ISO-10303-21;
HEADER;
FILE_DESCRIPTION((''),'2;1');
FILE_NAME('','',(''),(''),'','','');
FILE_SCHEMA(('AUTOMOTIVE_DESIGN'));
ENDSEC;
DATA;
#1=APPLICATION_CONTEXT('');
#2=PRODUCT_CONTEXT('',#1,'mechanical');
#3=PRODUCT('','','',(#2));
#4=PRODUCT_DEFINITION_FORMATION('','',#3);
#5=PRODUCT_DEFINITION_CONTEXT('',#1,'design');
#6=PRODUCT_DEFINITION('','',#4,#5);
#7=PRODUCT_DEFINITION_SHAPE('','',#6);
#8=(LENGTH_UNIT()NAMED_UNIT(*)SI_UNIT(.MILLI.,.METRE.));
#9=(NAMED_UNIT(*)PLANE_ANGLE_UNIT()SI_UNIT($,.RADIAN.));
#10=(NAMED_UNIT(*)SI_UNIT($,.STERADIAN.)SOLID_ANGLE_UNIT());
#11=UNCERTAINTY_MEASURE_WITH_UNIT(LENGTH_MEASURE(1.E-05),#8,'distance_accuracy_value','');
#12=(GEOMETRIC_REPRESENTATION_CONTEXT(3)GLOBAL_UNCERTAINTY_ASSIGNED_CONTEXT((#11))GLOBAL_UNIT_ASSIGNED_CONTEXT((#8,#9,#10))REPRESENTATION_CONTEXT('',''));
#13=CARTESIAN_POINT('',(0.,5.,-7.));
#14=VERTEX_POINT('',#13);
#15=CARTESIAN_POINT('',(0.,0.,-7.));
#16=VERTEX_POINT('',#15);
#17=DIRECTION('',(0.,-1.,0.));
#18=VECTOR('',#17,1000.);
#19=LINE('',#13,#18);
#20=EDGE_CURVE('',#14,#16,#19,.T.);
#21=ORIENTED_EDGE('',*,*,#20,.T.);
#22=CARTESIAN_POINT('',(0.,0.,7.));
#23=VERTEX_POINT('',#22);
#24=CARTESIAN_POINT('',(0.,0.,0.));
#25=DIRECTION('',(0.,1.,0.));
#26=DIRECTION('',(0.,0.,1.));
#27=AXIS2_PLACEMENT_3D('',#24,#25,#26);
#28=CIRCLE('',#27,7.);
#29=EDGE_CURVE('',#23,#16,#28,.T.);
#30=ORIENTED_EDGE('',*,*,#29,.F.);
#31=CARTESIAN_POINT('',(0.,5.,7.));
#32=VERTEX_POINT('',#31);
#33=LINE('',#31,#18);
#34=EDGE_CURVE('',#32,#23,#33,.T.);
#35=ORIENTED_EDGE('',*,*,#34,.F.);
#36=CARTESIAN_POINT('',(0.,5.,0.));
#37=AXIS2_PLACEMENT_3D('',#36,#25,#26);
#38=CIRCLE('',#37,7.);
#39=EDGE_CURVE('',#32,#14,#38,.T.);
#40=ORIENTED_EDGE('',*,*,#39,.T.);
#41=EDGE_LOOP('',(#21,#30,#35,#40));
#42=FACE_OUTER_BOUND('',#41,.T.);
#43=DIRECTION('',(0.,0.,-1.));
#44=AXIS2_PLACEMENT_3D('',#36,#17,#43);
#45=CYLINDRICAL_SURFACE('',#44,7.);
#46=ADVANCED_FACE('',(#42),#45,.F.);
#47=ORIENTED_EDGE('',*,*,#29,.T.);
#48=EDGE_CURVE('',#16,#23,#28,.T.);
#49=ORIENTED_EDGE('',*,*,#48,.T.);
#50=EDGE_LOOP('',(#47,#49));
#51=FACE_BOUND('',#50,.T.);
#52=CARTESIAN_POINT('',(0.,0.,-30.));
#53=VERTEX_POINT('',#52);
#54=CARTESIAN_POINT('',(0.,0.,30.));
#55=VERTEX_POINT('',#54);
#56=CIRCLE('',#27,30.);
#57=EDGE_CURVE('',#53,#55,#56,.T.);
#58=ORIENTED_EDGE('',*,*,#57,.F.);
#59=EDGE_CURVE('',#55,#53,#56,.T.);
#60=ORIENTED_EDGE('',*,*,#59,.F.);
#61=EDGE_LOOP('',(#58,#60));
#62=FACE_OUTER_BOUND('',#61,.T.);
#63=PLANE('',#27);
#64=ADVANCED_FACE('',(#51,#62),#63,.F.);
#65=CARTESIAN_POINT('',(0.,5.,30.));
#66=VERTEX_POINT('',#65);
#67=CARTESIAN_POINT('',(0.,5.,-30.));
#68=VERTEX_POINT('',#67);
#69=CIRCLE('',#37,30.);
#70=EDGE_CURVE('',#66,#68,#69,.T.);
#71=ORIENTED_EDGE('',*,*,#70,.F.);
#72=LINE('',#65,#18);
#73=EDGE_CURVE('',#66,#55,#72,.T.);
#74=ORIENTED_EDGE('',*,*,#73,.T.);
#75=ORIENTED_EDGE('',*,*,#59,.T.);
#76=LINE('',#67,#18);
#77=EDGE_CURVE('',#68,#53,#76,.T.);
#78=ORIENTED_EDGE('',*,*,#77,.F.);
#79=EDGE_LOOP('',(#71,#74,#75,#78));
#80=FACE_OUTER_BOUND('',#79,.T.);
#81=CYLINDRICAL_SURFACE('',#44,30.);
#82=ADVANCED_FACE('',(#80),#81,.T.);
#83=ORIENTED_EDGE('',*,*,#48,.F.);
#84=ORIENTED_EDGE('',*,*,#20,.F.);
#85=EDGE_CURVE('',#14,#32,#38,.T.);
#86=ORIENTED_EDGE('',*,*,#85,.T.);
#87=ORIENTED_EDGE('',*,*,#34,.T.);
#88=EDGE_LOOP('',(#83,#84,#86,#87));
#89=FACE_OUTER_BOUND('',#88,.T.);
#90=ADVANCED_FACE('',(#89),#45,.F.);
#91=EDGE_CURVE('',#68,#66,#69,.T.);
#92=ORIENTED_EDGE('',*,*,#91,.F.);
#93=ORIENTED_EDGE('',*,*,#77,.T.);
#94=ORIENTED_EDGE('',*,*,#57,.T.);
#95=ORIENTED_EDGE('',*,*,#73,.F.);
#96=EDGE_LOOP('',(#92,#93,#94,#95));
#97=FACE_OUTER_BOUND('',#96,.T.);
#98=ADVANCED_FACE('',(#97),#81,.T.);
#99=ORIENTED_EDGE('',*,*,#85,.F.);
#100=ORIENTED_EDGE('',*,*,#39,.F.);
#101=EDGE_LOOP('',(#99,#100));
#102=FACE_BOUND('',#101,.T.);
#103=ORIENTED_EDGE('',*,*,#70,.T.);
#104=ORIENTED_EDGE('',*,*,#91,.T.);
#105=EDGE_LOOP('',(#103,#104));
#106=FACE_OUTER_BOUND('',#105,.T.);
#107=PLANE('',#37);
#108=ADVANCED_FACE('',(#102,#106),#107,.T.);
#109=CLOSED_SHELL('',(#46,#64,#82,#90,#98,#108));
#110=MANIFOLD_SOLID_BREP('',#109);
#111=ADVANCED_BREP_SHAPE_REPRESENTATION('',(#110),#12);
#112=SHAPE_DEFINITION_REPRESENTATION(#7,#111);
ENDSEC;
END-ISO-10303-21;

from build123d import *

# Parameters (mm, degrees)
SKETCH_1_R          = 30
SKETCH_1_R_2        = 7
BOSS_EXTRUDE1_DEPTH = 5


with BuildPart() as part:
    # Sketch 1 → Boss-Extrude1 (new body)
    with BuildSketch(Plane(origin=(0, 0, 0), x_dir=(1, 0, 0), z_dir=(0, 1, 0))):
        with Locations(Location((0, 0, 0), (0, 0, 270))):
            Circle(SKETCH_1_R)
        with Locations(Location((0, 0, 0), (0, 0, 270))):
            Circle(SKETCH_1_R_2, mode=Mode.SUBTRACT)
    extrude(amount=BOSS_EXTRUDE1_DEPTH)


solid = part.part
